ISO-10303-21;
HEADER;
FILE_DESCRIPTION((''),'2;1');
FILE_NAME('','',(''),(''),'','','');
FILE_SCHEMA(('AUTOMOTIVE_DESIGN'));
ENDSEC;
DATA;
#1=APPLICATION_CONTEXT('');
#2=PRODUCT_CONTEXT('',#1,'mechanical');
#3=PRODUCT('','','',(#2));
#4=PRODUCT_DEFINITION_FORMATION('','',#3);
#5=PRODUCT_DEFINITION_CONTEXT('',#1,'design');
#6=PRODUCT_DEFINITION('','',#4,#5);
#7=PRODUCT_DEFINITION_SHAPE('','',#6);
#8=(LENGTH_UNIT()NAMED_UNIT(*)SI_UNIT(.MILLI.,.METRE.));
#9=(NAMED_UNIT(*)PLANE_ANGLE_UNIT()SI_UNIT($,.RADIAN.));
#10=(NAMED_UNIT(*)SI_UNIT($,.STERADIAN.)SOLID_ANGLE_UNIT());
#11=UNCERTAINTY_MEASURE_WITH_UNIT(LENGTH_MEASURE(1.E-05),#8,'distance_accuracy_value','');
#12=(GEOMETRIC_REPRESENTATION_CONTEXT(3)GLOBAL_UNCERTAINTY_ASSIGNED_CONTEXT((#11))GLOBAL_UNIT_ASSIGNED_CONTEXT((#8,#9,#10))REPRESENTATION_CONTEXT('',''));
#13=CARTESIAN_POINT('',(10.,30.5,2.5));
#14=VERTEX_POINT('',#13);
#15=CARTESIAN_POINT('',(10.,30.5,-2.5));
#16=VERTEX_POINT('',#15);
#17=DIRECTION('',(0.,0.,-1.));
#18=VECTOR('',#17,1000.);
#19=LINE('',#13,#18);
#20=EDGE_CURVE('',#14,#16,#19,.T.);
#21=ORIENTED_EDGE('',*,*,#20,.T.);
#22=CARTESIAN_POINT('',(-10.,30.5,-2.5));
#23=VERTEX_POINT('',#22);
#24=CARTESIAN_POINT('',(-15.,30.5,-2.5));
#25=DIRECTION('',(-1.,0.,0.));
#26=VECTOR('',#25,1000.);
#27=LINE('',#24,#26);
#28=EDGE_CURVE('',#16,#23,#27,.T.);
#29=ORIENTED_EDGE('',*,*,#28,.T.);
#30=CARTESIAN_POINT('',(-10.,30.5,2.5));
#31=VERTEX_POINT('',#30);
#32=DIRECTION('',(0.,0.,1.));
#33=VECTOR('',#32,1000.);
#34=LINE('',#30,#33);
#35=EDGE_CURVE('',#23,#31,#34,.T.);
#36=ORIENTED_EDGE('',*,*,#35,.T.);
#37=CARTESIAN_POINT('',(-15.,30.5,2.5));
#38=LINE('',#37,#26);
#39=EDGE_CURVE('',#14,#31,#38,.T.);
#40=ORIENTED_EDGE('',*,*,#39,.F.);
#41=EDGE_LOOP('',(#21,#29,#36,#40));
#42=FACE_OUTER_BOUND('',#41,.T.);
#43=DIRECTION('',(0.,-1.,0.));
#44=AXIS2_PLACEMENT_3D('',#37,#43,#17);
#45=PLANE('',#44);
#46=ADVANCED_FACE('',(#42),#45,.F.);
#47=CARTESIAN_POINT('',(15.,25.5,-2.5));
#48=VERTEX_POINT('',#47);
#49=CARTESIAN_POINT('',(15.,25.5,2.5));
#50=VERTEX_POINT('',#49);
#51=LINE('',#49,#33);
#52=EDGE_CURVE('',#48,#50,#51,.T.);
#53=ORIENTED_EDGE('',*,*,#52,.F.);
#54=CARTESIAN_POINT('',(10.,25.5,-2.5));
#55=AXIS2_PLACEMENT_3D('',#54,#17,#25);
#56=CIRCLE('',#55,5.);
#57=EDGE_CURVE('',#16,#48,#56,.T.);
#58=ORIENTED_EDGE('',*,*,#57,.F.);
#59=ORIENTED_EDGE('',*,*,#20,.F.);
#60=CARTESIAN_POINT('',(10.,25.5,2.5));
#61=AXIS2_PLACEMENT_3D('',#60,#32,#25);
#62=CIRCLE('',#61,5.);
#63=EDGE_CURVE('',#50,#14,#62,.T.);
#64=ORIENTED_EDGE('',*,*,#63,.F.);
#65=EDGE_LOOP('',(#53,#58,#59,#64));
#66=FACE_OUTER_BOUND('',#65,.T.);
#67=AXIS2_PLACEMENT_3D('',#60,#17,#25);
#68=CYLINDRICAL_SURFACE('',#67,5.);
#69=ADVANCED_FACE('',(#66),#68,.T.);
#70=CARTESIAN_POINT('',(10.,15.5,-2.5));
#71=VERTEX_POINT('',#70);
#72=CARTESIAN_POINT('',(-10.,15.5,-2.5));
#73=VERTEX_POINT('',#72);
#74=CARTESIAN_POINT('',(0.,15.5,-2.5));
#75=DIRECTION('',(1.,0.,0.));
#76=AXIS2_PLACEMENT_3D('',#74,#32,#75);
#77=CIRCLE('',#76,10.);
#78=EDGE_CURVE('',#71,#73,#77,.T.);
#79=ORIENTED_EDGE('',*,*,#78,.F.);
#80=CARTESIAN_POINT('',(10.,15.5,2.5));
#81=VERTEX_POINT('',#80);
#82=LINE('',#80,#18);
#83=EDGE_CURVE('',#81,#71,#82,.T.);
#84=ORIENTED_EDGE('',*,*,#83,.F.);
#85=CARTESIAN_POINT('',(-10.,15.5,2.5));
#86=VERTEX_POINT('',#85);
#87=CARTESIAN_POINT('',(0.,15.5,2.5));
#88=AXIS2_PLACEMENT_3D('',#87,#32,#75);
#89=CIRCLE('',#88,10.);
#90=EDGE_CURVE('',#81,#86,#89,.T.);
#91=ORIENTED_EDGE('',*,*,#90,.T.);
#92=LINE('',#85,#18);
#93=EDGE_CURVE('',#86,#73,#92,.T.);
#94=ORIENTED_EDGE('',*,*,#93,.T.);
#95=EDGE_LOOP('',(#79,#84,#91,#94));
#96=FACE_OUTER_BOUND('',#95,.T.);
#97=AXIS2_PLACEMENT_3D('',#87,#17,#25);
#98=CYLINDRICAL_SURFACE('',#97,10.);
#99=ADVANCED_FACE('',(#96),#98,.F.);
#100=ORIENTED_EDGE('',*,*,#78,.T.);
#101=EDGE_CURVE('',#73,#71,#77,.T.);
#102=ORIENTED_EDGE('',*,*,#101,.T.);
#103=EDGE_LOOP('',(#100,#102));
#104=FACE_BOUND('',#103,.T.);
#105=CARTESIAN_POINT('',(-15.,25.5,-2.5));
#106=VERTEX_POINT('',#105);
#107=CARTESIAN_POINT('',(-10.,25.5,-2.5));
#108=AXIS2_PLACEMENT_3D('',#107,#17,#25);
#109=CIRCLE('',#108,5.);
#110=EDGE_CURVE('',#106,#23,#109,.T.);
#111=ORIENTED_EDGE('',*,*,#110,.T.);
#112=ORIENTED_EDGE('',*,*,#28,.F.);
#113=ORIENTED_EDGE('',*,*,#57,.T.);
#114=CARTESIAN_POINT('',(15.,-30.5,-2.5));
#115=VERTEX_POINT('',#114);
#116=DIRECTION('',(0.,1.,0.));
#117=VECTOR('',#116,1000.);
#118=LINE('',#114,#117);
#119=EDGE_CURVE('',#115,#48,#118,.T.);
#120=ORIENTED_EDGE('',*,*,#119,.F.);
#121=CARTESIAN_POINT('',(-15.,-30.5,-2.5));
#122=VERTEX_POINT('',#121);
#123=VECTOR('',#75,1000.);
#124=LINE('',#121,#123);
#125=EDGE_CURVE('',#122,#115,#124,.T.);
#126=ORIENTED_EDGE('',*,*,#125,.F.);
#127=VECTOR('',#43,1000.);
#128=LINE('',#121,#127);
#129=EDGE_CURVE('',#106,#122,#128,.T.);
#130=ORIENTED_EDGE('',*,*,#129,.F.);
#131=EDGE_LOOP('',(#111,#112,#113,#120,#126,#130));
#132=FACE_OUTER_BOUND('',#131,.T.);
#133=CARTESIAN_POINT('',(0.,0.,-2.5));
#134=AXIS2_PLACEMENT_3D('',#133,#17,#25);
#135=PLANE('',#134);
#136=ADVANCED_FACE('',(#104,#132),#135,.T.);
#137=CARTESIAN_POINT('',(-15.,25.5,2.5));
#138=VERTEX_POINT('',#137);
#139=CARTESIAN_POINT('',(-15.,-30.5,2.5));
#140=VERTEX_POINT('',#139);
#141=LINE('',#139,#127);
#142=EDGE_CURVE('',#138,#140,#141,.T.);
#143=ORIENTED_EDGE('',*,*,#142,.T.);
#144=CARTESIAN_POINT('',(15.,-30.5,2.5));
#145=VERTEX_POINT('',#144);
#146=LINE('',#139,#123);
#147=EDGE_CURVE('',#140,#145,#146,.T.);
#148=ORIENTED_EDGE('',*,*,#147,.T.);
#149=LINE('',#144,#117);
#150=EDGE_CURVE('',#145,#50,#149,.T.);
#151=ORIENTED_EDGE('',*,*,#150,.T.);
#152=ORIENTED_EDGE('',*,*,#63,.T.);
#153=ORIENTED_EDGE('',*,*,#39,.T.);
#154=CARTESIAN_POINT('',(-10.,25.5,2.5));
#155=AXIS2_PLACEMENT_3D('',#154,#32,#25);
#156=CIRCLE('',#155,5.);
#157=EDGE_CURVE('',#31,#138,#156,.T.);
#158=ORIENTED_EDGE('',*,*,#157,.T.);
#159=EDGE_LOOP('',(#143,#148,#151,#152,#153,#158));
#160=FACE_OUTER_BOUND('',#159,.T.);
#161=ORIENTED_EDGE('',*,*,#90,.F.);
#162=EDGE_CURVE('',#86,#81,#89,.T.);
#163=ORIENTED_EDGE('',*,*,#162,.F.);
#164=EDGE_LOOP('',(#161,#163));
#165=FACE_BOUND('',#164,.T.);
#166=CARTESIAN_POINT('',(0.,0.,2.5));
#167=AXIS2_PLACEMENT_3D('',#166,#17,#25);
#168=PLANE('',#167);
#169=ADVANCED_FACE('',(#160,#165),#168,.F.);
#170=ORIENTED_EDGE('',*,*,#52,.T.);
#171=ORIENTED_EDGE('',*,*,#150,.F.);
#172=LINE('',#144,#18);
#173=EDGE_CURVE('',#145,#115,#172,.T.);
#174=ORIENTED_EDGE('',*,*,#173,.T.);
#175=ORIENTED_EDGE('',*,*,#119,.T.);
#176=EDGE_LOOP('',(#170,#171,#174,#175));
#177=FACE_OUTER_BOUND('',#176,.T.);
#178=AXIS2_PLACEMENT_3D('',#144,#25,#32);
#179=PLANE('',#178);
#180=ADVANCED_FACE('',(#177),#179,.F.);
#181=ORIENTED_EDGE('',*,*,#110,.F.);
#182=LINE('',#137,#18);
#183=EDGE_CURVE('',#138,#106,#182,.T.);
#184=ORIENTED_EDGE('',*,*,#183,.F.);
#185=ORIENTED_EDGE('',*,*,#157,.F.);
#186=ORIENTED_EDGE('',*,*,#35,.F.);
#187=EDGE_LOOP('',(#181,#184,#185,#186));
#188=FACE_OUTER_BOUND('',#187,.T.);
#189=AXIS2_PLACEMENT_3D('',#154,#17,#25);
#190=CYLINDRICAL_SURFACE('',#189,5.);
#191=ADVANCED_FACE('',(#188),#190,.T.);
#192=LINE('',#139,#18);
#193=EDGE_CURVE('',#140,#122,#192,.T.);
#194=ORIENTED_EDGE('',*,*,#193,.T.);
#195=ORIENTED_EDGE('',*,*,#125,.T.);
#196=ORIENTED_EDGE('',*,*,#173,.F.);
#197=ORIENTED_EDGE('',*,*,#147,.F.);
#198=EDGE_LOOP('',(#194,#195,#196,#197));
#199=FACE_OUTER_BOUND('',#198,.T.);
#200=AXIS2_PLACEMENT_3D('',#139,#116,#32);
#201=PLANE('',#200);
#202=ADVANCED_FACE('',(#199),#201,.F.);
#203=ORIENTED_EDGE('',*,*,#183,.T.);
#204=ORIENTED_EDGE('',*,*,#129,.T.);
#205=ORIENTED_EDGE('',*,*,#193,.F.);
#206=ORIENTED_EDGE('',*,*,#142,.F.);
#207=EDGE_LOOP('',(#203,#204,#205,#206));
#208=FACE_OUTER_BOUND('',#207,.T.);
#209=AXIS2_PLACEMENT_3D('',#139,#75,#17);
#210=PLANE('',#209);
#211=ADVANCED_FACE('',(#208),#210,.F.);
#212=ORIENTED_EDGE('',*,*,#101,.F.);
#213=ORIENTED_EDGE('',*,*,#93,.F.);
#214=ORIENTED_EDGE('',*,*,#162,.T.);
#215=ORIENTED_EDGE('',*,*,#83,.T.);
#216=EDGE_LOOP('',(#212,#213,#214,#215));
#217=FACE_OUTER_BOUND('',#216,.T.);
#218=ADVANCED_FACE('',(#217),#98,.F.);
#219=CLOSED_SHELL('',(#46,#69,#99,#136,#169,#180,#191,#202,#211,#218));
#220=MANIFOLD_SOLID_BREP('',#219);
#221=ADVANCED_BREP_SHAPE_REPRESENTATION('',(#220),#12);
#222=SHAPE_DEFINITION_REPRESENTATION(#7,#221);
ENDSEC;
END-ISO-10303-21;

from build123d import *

# Parameters (mm, degrees)
SKETCH_1_W      = 30
SKETCH_1_H      = 61
SKETCH_1_R      = 10
EXTRUDE_1_DEPTH = 2.5
FILLET_1_R      = 5


with BuildPart() as part:
    # 草图1 → 凸台-拉伸1 (new, symmetric)
    with BuildSketch(Plane.XY):
        Rectangle(SKETCH_1_W, SKETCH_1_H)
        with Locations((0, 15.5)):
            Circle(SKETCH_1_R, mode=Mode.SUBTRACT)
    extrude(amount=EXTRUDE_1_DEPTH, both=True)

    # 圆角1
    fillet_1_edges = [part.edges().sort_by_distance(p)[0] for p in [
        (-15, 30.5, 0),
        (15, 30.5, 0),
    ]]
    fillet(fillet_1_edges, radius=FILLET_1_R)


solid = part.part
